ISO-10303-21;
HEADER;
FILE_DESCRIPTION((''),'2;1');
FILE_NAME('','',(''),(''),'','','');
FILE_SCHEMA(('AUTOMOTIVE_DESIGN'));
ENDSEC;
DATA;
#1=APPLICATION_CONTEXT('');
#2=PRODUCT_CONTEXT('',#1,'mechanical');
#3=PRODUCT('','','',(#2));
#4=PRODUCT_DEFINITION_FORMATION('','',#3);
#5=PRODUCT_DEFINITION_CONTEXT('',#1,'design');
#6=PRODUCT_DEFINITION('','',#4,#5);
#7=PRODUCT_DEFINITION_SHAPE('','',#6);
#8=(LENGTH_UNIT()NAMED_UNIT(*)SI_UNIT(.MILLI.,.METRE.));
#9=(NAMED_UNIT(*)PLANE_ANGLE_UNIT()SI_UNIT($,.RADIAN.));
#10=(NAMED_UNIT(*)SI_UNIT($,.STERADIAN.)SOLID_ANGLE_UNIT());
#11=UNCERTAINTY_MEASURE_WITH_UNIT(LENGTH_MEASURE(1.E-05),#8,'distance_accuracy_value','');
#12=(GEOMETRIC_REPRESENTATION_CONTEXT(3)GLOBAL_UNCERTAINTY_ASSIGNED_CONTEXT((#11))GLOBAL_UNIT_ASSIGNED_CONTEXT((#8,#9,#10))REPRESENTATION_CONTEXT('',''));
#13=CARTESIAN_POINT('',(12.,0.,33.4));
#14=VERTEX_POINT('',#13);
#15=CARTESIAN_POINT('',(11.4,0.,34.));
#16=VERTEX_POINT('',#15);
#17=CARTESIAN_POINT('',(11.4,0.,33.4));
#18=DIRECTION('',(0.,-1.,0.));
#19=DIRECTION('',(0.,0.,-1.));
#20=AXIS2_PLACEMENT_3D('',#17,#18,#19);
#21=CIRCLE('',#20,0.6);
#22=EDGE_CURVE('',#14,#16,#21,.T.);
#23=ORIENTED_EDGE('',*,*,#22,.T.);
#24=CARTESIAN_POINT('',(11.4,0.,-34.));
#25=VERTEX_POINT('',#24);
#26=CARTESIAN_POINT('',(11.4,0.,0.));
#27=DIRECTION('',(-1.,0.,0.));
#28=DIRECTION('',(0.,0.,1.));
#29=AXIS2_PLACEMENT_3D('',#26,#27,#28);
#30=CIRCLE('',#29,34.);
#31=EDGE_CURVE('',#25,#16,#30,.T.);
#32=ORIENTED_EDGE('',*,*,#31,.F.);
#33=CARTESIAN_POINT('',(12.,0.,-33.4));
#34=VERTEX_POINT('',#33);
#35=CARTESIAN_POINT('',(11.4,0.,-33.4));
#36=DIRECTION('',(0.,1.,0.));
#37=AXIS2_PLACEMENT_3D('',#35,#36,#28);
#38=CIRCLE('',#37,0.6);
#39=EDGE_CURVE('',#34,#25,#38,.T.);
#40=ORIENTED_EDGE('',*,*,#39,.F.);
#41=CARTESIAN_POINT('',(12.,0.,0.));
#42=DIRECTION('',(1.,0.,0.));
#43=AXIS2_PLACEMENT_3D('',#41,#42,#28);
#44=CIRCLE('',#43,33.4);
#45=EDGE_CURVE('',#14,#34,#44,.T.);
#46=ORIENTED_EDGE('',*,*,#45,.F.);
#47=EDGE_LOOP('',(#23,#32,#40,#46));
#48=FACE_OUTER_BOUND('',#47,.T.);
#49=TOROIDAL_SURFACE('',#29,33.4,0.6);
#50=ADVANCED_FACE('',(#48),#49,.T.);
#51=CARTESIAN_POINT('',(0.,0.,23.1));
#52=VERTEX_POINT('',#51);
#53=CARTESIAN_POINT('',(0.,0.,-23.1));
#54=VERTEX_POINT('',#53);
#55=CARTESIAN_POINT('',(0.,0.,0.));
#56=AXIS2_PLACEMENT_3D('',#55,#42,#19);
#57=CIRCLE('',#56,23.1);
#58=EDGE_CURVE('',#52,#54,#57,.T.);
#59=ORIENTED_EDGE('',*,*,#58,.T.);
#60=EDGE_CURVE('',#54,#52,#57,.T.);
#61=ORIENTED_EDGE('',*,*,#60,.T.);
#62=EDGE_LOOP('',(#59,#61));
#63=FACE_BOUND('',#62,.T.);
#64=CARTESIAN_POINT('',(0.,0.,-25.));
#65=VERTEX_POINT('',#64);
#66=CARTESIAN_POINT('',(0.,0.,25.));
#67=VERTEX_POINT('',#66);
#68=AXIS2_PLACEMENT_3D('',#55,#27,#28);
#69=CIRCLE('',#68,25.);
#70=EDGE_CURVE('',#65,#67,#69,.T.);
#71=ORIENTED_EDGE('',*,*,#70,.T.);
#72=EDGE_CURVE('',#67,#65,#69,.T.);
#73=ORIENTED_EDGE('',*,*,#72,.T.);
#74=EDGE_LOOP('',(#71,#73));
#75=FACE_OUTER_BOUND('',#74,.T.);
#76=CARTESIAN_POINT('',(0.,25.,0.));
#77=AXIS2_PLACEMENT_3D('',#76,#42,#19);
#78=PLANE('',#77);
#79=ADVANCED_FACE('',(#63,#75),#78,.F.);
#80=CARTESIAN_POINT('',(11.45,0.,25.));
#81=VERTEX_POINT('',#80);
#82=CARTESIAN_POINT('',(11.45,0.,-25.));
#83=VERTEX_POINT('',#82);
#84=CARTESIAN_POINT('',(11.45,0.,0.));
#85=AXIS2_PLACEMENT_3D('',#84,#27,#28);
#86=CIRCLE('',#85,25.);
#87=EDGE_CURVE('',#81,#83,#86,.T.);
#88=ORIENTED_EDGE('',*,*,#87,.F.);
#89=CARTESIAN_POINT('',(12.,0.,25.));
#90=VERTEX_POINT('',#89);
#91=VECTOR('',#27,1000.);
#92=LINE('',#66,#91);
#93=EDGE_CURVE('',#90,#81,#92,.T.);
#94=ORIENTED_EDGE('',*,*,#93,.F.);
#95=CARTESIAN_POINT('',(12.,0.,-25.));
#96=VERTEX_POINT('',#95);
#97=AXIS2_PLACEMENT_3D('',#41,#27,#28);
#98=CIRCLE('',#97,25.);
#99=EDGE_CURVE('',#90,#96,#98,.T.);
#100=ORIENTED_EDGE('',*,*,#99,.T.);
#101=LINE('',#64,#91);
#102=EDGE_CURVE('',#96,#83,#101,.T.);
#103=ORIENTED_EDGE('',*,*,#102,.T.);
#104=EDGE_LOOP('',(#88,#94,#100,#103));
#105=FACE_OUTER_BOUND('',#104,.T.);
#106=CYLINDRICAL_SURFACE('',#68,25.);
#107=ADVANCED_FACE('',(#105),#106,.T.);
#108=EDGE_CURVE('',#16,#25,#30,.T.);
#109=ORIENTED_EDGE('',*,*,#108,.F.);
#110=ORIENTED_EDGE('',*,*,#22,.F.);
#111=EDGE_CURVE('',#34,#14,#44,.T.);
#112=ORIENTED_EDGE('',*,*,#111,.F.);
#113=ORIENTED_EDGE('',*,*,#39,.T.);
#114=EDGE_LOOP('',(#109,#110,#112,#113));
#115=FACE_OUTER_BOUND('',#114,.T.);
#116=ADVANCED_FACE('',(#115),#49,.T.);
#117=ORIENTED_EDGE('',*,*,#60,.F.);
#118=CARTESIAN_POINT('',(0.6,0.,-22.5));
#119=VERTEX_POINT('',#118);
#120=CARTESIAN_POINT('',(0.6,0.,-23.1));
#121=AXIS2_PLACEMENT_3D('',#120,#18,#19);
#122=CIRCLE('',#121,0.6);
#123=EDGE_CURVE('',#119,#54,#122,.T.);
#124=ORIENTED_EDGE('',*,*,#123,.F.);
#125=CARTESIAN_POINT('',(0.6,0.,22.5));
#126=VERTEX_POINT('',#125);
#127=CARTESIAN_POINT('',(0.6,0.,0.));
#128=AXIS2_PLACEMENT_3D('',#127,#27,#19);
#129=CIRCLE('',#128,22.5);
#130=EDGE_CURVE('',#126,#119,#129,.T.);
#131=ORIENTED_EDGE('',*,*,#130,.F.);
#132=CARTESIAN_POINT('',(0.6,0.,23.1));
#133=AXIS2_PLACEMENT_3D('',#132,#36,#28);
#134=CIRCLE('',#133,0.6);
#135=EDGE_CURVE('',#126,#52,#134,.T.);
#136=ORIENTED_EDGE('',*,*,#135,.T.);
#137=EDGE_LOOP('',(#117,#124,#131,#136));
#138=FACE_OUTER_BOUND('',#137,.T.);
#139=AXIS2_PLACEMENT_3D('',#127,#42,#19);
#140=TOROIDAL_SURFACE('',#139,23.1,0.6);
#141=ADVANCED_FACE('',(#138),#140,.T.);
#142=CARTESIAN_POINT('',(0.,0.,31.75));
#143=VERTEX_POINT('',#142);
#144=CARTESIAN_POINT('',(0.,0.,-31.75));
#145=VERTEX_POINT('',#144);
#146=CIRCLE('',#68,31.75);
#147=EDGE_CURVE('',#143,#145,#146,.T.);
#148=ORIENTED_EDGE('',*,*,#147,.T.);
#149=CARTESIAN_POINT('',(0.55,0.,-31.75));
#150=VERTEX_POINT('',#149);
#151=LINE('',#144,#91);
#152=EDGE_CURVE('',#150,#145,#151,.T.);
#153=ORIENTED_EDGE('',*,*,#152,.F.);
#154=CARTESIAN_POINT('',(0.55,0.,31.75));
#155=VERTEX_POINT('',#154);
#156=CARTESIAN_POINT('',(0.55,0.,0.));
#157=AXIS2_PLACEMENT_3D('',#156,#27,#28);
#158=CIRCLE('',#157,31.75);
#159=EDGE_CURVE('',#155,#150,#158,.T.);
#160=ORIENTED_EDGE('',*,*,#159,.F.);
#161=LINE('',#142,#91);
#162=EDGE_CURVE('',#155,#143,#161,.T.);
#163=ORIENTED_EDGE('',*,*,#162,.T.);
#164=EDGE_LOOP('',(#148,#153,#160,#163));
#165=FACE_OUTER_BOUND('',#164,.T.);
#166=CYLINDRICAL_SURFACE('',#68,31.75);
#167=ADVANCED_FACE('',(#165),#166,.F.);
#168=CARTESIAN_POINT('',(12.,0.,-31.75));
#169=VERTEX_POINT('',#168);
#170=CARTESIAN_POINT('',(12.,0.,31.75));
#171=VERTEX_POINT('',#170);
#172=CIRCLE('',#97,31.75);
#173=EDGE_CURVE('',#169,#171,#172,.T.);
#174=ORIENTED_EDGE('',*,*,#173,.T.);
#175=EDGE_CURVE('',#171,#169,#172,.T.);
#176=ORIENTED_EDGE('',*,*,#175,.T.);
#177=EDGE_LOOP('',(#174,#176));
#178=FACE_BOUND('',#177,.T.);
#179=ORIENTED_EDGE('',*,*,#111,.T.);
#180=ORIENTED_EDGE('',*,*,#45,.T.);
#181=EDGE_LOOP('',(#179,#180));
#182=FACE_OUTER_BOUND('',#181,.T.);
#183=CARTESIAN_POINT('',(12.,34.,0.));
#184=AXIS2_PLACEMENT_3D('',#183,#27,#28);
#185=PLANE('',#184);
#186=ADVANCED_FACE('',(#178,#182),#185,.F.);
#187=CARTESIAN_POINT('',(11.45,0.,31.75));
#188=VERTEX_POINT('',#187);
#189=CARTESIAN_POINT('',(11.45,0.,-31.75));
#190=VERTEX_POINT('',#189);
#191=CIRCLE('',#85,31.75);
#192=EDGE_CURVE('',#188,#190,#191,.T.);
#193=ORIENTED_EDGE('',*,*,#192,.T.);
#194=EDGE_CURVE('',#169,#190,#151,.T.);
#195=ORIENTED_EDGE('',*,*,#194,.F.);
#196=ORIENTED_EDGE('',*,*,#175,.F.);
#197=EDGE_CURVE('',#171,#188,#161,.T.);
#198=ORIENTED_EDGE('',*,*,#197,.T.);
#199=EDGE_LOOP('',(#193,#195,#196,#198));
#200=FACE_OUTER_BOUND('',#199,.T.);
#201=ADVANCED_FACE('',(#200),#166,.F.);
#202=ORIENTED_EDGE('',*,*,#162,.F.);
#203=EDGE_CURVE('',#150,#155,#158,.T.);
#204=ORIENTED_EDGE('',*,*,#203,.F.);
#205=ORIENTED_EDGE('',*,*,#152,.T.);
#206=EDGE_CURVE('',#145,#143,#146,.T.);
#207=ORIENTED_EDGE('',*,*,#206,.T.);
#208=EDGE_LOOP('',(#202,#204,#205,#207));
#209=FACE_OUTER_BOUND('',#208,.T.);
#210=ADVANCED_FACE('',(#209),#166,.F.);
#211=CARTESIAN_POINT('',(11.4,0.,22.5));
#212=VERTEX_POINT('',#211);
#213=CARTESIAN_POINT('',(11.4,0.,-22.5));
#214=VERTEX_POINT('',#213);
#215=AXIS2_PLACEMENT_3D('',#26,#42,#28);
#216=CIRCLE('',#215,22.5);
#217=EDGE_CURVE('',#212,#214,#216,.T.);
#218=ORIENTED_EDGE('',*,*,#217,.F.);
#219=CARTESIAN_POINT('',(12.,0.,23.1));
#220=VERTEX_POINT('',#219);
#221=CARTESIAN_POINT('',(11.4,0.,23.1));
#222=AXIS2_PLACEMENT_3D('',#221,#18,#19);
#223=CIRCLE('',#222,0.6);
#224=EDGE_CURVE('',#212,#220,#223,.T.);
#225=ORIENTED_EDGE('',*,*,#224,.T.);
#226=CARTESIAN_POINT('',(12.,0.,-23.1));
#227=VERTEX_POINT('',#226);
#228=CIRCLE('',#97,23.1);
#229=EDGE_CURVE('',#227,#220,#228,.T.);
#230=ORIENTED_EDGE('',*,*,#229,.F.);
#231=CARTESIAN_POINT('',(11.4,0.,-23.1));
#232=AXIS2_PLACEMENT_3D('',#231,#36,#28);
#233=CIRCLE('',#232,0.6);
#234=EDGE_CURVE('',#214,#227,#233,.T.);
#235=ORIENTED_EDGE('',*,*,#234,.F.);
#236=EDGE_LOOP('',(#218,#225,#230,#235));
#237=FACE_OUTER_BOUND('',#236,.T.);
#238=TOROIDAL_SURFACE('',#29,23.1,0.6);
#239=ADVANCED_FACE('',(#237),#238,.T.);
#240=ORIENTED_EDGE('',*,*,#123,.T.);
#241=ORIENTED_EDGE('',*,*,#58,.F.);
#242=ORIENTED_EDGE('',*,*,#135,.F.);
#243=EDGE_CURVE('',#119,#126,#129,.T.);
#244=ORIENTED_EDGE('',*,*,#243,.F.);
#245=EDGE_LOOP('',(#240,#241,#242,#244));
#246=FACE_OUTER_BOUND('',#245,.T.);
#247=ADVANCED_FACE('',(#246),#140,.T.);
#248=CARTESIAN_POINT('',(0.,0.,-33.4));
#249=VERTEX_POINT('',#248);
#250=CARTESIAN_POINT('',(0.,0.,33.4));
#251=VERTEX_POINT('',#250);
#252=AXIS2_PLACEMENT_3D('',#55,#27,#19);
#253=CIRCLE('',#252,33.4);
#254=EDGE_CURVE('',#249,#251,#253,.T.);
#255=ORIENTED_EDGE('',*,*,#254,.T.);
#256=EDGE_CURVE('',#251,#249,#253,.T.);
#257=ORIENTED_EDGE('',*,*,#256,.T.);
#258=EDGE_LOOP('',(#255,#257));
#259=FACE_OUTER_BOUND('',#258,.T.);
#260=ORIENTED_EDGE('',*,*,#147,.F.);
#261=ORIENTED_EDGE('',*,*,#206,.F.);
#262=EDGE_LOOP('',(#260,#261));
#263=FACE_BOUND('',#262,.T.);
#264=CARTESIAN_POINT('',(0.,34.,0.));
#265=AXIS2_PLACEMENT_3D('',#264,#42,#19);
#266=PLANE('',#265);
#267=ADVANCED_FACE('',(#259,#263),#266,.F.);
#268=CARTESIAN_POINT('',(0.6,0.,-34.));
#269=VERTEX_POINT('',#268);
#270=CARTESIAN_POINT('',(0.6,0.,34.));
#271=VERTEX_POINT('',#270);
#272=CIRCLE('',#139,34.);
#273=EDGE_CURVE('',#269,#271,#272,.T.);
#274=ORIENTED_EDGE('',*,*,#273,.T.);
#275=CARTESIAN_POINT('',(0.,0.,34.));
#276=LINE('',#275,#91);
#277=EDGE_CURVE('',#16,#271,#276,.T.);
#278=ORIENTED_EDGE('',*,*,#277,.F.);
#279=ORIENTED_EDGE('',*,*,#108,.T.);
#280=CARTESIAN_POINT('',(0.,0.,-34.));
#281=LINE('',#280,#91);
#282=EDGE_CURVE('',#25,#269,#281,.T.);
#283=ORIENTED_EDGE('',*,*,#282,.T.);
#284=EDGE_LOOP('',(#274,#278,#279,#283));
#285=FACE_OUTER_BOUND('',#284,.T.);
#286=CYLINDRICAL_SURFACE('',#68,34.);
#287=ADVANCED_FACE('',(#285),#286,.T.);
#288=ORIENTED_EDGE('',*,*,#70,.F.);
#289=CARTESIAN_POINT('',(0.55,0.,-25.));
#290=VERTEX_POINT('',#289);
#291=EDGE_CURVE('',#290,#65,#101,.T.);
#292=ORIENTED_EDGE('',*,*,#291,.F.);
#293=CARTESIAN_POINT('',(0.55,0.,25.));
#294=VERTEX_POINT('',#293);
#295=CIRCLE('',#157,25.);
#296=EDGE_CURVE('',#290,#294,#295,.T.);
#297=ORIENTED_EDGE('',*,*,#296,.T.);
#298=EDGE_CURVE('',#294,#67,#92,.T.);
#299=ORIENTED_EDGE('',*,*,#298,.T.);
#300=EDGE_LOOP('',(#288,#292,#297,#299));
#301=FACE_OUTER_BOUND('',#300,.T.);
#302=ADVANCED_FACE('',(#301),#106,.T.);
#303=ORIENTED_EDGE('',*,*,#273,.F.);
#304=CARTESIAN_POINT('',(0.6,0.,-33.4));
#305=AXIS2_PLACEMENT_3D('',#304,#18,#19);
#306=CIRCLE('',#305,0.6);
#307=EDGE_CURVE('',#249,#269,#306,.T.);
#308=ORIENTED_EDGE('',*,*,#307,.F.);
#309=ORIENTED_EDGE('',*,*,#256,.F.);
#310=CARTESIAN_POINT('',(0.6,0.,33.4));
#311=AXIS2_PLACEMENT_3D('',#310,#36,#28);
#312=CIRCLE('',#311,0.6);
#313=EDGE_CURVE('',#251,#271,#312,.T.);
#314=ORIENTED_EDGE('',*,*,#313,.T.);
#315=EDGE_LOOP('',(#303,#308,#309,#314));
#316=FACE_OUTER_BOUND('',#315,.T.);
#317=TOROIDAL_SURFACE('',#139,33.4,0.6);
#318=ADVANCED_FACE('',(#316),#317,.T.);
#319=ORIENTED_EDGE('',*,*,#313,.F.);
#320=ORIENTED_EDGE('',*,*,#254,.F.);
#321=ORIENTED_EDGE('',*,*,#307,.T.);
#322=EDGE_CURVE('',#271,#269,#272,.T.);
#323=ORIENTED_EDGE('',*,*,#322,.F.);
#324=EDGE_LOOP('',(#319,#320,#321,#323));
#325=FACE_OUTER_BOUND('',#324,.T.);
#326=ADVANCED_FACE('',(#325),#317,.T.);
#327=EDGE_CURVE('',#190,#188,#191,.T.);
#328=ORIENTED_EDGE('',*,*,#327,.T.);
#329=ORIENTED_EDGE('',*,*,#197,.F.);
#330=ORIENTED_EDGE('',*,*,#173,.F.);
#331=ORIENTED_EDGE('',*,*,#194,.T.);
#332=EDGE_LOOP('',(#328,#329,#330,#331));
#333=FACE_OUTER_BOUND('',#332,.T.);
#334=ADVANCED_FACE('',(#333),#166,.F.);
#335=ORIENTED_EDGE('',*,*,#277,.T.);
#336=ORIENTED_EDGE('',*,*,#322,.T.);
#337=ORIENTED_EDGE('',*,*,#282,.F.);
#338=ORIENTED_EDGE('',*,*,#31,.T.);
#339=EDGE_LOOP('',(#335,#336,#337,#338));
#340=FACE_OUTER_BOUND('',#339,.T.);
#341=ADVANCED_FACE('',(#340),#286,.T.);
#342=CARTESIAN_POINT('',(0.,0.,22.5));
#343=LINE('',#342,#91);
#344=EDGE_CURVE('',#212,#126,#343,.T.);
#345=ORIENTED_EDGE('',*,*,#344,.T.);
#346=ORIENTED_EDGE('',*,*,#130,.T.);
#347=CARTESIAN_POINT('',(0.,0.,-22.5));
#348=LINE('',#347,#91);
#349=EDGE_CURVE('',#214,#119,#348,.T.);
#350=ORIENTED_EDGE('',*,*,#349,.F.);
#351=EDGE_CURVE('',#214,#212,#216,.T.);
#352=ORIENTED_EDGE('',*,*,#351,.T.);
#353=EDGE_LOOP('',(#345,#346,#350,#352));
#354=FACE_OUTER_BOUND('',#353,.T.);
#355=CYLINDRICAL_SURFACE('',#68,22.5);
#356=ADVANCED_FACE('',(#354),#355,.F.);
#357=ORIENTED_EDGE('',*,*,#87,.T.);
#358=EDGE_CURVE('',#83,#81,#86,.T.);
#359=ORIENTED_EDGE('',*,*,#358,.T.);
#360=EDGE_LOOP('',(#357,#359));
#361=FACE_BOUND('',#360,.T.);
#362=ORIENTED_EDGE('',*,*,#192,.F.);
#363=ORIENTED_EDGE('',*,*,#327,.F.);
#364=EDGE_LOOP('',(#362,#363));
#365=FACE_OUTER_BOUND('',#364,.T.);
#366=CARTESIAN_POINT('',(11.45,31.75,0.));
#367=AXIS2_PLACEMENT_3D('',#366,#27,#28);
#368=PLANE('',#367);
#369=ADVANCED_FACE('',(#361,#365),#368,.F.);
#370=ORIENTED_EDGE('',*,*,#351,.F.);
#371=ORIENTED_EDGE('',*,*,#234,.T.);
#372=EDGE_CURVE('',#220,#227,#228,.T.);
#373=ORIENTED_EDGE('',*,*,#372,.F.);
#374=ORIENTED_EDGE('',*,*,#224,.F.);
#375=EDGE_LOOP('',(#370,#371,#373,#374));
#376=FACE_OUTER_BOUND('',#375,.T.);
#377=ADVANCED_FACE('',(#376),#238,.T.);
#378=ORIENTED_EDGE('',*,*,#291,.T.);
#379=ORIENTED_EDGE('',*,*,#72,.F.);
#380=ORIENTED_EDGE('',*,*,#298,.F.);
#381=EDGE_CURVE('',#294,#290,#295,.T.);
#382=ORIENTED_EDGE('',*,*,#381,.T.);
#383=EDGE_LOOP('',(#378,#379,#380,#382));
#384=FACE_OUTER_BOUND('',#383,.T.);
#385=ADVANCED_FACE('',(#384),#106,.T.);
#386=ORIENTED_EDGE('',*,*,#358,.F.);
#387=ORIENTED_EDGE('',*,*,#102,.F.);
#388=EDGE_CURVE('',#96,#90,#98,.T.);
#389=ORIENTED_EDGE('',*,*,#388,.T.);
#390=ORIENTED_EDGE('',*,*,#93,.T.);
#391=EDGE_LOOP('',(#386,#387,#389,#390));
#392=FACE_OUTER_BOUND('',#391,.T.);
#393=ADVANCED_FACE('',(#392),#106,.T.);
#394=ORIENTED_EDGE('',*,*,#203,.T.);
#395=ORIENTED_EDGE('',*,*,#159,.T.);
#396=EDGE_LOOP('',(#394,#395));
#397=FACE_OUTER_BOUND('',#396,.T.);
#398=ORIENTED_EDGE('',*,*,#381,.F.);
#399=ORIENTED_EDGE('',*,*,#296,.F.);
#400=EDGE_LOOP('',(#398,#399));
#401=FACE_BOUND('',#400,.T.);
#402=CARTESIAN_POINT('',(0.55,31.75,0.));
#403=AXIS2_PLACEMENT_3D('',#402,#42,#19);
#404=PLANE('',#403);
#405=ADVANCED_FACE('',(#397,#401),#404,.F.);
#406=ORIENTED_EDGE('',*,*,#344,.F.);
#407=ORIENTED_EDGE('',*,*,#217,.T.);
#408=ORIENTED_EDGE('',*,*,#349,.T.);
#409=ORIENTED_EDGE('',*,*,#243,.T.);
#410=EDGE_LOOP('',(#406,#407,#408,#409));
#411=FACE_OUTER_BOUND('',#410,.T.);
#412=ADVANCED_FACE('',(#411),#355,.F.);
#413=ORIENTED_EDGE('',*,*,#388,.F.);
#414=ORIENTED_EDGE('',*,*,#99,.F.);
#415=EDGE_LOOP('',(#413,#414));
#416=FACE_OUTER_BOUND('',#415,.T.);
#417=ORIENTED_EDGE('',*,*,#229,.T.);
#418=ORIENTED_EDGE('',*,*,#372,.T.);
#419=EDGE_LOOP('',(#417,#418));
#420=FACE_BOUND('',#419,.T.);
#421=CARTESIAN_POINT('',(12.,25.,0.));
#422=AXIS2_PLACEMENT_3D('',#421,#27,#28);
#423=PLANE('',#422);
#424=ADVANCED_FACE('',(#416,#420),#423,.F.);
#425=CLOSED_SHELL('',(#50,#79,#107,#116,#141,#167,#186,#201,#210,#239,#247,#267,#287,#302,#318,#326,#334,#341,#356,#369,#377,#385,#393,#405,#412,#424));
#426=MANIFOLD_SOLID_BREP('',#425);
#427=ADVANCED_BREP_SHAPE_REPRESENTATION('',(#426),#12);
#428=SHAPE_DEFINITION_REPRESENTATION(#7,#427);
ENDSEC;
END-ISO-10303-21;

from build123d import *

# Parameters (mm, degrees)
FILLET1_R = 0.6
FILLET2_R = 0.6


with BuildPart() as part:
    # Sketch1 → Revolve1 (revolve)
    with BuildSketch(Plane.XY, mode=Mode.PRIVATE) as revolve1_sk:
        Polygon((0, 22.5), (12, 22.5), (12, 25), (11.45, 25), (11.45, 31.75), (12, 31.75), (12, 34), (0, 34), (0, 31.75), (0.55, 31.75), (0.55, 25), (0, 25), align=None)
    revolve(revolve1_sk.sketch.rotate(Axis((0, 0, 0), (1, 0, 0)), 90), axis=Axis((0, 0, 0), (1, 0, 0)))

    # Fillet1
    fillet1_edges = [part.edges().sort_by_distance(p)[0] for p in [
        (0, 0, -34),
        (12, 0, -34),
    ]]
    fillet(fillet1_edges, radius=FILLET1_R)

    # Fillet2
    fillet2_edges = [part.edges().sort_by_distance(p)[0] for p in [
        (12, 0, -22.5),
        (0, 0, -22.5),
    ]]
    fillet(fillet2_edges, radius=FILLET2_R)


solid = part.part
